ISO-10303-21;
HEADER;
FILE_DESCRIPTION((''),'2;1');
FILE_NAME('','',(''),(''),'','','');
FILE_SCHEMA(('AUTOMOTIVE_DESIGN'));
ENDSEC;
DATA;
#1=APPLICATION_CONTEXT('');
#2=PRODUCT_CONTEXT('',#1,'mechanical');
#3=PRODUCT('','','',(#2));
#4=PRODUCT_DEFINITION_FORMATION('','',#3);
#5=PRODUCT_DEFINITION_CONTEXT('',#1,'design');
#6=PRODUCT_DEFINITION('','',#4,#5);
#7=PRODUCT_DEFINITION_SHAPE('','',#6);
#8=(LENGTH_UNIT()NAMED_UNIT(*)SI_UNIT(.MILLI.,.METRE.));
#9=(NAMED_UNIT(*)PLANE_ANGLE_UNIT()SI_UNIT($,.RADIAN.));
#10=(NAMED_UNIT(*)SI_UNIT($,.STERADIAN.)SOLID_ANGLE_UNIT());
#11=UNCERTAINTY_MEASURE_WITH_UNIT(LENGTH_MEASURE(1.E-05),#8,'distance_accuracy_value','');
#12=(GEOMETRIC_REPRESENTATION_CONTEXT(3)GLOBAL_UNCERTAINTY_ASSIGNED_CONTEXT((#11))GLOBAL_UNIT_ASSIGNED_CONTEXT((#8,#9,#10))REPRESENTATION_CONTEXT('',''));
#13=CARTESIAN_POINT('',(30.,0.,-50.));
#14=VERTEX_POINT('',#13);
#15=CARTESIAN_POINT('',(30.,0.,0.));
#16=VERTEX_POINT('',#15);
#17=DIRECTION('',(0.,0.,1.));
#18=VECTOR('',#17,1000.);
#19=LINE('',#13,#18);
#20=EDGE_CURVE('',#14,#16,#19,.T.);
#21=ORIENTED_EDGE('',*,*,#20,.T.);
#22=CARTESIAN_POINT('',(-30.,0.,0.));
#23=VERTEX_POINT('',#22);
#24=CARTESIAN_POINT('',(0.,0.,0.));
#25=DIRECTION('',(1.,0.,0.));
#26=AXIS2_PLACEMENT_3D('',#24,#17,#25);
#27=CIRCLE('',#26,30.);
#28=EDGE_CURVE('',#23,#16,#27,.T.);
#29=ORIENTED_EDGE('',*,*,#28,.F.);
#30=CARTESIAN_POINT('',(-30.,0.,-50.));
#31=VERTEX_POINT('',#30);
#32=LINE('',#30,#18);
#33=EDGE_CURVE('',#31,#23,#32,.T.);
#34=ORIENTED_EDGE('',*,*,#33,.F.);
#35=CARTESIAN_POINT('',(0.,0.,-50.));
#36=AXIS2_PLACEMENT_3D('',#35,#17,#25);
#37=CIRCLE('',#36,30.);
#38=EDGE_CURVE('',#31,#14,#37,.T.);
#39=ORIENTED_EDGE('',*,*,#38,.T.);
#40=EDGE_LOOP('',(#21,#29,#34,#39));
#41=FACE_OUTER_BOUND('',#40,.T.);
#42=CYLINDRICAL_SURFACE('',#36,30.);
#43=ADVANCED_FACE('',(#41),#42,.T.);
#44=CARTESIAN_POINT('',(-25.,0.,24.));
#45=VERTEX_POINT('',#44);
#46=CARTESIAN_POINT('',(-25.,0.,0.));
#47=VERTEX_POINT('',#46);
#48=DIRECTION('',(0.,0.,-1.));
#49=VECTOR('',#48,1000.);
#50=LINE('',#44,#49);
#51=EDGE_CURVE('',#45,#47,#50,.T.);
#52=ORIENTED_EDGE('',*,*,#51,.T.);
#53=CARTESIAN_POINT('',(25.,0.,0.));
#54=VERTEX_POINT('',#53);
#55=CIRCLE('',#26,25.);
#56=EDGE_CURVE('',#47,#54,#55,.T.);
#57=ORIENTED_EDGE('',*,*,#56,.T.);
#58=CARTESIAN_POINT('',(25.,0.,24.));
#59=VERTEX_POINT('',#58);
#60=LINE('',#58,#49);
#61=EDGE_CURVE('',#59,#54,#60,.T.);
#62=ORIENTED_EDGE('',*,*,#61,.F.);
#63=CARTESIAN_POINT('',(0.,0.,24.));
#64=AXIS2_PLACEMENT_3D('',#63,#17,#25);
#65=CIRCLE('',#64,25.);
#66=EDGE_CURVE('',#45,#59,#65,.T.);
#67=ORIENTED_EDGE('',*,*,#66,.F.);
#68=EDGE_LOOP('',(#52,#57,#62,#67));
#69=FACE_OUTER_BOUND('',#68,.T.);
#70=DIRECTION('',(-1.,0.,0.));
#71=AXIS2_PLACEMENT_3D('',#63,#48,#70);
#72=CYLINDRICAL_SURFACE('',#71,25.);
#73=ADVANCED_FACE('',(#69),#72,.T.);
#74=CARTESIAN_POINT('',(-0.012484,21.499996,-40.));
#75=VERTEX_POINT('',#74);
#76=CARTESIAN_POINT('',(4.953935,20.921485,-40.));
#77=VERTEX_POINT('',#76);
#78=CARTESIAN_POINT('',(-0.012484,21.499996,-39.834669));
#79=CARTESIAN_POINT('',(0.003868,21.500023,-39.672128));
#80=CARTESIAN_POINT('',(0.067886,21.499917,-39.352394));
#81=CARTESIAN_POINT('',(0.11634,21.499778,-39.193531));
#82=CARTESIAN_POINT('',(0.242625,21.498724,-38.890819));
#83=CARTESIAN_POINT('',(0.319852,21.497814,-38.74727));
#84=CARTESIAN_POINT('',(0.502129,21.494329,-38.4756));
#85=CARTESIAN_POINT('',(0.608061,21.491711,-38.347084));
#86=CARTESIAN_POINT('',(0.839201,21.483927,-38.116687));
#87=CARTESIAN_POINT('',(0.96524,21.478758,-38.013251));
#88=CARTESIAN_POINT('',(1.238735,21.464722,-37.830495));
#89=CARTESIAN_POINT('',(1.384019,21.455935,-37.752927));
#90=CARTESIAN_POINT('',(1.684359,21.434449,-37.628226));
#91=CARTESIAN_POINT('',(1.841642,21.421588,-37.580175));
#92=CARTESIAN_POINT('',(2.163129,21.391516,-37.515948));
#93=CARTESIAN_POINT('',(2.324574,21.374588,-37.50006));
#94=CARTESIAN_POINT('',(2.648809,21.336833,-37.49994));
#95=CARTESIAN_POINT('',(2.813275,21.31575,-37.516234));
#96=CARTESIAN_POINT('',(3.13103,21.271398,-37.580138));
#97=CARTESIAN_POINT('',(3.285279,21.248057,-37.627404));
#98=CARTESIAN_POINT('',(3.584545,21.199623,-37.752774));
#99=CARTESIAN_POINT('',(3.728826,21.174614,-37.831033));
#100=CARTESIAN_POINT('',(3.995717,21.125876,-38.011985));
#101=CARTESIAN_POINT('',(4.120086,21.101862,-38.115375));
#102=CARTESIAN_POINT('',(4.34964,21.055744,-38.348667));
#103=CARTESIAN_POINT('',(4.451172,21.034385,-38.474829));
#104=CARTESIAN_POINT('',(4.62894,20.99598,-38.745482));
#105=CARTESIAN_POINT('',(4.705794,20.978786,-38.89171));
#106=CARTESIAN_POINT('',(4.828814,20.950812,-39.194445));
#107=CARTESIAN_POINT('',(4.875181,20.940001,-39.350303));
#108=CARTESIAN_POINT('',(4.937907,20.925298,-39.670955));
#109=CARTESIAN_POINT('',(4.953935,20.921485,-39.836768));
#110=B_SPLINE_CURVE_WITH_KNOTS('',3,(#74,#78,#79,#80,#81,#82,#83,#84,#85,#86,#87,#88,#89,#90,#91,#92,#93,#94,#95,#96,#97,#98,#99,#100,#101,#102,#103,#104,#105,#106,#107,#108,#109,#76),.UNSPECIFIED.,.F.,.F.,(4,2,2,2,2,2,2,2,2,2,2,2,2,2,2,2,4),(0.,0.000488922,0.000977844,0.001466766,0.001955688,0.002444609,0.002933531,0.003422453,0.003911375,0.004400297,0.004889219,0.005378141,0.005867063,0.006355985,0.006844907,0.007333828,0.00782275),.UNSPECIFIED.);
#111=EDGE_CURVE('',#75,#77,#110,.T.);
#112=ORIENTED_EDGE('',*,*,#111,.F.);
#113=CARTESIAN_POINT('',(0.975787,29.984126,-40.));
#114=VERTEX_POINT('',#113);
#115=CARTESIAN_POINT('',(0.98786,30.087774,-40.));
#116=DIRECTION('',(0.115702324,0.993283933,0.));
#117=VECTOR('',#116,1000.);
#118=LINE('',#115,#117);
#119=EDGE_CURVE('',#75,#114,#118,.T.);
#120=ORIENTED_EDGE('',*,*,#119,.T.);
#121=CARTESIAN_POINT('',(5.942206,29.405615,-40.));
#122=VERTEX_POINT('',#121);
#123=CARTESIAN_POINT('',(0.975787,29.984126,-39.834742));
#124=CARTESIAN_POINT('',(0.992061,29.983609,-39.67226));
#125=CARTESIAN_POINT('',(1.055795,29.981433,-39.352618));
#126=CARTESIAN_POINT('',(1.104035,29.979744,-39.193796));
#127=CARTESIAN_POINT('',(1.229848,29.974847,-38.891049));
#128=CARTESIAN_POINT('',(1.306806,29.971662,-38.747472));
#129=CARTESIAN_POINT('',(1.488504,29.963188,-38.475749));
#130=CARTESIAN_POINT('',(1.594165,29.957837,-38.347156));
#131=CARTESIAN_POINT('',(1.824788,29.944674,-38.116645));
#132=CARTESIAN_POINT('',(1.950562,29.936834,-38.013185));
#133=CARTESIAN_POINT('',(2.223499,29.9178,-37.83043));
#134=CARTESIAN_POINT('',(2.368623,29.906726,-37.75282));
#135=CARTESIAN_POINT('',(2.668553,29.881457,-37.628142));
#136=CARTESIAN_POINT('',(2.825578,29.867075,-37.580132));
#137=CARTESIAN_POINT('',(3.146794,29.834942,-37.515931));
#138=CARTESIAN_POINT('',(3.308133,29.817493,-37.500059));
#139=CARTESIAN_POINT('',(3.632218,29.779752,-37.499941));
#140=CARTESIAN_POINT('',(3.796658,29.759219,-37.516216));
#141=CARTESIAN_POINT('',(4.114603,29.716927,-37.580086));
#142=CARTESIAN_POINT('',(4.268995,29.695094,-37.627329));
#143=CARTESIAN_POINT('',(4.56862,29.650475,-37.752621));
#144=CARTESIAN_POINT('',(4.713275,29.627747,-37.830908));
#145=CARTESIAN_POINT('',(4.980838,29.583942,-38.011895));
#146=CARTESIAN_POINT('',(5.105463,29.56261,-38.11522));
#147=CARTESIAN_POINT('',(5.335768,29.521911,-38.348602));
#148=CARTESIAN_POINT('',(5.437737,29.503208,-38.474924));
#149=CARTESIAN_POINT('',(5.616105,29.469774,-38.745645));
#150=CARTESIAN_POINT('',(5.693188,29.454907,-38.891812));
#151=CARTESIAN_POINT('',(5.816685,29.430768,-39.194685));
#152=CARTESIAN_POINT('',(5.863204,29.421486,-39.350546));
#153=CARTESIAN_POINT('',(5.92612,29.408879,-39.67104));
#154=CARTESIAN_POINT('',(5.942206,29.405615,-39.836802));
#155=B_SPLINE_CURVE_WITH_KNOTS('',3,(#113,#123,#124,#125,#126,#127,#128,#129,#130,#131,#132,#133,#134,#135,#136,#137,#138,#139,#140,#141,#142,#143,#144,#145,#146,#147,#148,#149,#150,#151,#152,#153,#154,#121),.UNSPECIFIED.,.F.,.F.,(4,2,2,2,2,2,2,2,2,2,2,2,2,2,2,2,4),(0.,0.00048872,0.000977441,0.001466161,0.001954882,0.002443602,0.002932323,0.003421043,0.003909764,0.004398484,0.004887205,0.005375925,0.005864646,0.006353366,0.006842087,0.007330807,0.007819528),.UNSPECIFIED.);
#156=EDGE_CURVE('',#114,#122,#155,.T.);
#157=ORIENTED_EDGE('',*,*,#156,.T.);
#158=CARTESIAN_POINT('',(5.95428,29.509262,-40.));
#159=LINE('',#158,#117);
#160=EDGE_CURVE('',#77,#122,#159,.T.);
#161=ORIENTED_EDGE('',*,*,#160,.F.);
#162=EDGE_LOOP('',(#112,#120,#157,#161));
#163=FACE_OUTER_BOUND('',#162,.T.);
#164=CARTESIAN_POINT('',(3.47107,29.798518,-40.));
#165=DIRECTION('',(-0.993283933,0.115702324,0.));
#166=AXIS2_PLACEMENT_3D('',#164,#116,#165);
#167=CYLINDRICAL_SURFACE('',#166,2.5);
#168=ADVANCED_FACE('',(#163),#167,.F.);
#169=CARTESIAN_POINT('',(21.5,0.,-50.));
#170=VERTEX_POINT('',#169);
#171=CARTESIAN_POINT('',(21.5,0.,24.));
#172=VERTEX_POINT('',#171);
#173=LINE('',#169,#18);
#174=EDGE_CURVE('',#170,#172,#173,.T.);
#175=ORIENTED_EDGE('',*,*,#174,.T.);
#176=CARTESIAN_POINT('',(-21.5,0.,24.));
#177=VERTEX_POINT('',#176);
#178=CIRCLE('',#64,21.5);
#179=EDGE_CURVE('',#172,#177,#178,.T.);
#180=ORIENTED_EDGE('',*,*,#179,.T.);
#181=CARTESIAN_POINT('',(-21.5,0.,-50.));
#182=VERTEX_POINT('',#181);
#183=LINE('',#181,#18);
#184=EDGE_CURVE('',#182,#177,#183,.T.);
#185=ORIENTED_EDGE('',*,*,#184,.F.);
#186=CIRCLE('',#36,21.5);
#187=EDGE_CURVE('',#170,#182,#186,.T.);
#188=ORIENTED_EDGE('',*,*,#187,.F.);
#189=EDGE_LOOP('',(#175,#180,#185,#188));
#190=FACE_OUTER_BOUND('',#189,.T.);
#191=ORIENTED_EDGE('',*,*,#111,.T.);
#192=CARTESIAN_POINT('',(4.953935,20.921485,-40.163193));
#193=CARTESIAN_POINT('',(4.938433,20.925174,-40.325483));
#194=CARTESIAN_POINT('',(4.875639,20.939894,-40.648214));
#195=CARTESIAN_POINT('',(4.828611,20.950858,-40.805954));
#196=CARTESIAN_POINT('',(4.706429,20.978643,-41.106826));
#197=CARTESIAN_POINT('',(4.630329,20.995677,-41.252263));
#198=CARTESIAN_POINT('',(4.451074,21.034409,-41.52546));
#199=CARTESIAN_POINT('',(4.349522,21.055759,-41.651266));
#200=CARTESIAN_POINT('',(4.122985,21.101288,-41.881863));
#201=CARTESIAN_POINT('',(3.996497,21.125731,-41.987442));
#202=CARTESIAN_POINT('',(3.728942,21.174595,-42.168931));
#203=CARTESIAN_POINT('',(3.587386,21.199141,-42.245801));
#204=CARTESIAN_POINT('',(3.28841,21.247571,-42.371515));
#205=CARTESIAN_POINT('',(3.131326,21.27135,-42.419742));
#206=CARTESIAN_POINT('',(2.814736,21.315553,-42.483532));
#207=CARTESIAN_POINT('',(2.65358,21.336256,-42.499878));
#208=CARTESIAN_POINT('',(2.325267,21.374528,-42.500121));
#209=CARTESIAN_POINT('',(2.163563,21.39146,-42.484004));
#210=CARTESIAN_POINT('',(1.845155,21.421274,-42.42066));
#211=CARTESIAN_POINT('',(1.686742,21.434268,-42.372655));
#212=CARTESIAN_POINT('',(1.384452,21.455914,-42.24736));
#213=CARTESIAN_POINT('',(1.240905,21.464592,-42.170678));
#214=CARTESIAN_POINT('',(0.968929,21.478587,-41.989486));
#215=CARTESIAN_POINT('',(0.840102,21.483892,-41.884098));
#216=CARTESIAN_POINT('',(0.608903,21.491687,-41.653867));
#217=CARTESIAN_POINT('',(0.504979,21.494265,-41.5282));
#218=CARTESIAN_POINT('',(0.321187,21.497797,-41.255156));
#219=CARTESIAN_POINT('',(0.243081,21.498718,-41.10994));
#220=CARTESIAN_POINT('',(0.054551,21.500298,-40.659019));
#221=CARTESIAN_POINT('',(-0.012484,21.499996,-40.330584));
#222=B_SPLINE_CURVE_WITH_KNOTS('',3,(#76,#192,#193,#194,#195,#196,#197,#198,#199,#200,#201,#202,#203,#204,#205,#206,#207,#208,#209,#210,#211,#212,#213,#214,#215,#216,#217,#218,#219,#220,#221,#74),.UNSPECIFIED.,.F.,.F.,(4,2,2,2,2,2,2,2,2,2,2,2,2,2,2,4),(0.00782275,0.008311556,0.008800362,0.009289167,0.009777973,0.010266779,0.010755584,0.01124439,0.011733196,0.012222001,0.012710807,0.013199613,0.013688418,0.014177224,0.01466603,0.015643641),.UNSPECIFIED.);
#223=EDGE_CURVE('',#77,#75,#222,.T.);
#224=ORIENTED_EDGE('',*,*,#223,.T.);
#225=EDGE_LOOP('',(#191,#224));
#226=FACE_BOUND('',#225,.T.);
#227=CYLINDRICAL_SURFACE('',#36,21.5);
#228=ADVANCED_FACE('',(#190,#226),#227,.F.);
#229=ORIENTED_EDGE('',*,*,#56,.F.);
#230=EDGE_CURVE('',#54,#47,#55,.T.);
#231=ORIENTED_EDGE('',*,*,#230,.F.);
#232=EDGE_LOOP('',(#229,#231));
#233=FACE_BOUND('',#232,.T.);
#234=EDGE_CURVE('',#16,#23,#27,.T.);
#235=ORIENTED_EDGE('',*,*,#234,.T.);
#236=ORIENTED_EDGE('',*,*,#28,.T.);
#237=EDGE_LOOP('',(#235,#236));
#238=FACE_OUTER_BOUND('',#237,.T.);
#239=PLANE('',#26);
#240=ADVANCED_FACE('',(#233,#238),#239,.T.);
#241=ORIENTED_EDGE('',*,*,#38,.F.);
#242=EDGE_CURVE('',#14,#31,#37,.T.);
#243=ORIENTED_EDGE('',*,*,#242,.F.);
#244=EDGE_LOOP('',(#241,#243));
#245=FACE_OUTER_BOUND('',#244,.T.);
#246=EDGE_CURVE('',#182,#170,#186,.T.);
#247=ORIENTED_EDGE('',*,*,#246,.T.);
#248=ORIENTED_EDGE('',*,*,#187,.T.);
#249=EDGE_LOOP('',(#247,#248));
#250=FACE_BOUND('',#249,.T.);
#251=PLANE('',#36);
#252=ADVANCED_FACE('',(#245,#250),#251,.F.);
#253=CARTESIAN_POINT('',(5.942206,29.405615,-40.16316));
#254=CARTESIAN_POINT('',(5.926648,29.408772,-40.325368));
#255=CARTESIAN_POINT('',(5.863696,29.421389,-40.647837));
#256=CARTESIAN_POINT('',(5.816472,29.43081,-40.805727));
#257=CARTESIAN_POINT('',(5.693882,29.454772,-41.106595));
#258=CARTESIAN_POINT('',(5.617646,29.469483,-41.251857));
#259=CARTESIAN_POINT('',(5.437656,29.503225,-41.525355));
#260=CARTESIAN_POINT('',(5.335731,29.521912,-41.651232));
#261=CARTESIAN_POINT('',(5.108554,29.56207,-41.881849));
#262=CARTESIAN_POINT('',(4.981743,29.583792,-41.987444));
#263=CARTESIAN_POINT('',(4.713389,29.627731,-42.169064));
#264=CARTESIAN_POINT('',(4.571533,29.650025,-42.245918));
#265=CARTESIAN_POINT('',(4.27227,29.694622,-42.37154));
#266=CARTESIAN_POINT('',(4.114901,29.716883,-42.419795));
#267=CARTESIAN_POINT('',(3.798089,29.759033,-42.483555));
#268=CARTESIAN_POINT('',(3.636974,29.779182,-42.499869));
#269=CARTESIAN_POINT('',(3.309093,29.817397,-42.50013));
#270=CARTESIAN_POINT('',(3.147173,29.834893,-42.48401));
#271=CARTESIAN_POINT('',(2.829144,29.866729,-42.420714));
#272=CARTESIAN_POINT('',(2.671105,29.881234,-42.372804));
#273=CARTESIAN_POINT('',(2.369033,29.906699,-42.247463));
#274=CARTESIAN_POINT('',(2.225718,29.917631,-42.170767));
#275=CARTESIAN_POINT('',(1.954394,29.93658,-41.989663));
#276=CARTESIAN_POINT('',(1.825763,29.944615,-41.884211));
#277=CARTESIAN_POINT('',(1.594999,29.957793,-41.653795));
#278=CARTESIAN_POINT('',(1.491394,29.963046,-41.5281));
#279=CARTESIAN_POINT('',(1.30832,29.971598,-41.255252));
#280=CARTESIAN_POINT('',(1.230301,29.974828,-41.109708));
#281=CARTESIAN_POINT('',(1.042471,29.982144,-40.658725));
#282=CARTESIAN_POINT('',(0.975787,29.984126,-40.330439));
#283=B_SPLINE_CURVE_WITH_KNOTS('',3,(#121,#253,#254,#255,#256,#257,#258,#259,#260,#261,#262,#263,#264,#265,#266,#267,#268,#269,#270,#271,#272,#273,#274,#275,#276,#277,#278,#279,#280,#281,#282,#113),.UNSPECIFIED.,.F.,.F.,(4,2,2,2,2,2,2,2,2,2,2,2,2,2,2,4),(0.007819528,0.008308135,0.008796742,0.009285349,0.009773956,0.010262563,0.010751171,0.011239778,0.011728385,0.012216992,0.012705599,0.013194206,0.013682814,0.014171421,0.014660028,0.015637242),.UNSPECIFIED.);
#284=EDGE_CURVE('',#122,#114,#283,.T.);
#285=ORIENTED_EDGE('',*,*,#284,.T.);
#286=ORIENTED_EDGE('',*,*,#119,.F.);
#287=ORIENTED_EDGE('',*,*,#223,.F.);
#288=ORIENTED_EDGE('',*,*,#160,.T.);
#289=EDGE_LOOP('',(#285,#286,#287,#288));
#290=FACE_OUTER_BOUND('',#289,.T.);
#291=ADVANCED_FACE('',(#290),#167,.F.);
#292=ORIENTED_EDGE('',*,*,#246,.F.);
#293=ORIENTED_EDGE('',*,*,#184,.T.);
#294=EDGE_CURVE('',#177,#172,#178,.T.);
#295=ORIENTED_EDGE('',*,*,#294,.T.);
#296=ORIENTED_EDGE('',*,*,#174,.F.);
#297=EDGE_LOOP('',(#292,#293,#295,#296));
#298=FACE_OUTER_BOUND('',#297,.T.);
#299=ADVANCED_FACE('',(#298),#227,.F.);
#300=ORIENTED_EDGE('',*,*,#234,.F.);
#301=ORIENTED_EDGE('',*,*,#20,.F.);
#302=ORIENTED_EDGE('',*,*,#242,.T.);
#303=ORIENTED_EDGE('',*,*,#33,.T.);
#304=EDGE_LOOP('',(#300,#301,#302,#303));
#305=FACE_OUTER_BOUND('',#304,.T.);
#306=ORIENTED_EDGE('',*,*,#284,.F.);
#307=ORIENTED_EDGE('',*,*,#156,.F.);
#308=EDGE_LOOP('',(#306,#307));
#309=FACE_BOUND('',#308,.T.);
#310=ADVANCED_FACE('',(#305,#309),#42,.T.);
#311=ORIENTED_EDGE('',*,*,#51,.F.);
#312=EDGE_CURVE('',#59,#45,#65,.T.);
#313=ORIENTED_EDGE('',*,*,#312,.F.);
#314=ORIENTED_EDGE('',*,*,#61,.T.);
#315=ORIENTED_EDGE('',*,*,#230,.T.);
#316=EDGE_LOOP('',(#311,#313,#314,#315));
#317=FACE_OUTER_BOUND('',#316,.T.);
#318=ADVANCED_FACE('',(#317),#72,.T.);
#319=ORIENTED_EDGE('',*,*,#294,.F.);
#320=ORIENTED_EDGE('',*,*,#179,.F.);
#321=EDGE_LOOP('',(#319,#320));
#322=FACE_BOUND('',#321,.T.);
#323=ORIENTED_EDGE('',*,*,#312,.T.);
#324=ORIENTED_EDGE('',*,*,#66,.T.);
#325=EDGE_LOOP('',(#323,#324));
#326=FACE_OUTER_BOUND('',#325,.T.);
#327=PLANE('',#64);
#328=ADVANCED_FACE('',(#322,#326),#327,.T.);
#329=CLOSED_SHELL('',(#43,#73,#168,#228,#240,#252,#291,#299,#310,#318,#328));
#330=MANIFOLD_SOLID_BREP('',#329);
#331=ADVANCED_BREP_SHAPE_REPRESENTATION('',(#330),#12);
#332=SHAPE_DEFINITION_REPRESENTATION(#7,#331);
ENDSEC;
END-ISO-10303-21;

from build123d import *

# Parameters (mm, degrees)
SKETCH1_R             = 30
SKETCH1_R_2           = 21.5
BOSS_EXTRUDE1_DEPTH   = 50
M6_TAPPED_HOLE1_D     = 5
M6_TAPPED_HOLE1_DEPTH = 18
M6_TAPPED_HOLE1_TIP   = 1.502151548
BOSS_EXTRUDE2_START   = 24
SKETCH4_R             = 25
SKETCH4_R_2           = 21.5
BOSS_EXTRUDE2_DEPTH   = 24


with BuildPart() as part:
    # Sketch1 → Boss-Extrude1 (new body)
    with BuildSketch(Plane.XY):
        Circle(SKETCH1_R)
        Circle(SKETCH1_R_2, mode=Mode.SUBTRACT)
    extrude(amount=-BOSS_EXTRUDE1_DEPTH)

    # M6 Tapped Hole1
    with Locations(Plane(origin=(3.471069712, 29.798518001, -40), x_dir=(0.993283933364, -0.115702323745, 0), z_dir=(0.115702323745, 0.993283933364, 0))):
        with Locations((0, 0)):
            Hole(M6_TAPPED_HOLE1_D / 2, depth=M6_TAPPED_HOLE1_DEPTH)
            with Locations((0, 0, -(M6_TAPPED_HOLE1_DEPTH + M6_TAPPED_HOLE1_TIP / 2))):  # 118° drill point
                Cone(0, M6_TAPPED_HOLE1_D / 2, M6_TAPPED_HOLE1_TIP, mode=Mode.SUBTRACT)

    # Sketch4 → Boss-Extrude2 (add)
    with BuildSketch(Plane.XY.offset(BOSS_EXTRUDE2_START)):
        Circle(SKETCH4_R)
        Circle(SKETCH4_R_2, mode=Mode.SUBTRACT)
    extrude(amount=-BOSS_EXTRUDE2_DEPTH)


solid = part.part
